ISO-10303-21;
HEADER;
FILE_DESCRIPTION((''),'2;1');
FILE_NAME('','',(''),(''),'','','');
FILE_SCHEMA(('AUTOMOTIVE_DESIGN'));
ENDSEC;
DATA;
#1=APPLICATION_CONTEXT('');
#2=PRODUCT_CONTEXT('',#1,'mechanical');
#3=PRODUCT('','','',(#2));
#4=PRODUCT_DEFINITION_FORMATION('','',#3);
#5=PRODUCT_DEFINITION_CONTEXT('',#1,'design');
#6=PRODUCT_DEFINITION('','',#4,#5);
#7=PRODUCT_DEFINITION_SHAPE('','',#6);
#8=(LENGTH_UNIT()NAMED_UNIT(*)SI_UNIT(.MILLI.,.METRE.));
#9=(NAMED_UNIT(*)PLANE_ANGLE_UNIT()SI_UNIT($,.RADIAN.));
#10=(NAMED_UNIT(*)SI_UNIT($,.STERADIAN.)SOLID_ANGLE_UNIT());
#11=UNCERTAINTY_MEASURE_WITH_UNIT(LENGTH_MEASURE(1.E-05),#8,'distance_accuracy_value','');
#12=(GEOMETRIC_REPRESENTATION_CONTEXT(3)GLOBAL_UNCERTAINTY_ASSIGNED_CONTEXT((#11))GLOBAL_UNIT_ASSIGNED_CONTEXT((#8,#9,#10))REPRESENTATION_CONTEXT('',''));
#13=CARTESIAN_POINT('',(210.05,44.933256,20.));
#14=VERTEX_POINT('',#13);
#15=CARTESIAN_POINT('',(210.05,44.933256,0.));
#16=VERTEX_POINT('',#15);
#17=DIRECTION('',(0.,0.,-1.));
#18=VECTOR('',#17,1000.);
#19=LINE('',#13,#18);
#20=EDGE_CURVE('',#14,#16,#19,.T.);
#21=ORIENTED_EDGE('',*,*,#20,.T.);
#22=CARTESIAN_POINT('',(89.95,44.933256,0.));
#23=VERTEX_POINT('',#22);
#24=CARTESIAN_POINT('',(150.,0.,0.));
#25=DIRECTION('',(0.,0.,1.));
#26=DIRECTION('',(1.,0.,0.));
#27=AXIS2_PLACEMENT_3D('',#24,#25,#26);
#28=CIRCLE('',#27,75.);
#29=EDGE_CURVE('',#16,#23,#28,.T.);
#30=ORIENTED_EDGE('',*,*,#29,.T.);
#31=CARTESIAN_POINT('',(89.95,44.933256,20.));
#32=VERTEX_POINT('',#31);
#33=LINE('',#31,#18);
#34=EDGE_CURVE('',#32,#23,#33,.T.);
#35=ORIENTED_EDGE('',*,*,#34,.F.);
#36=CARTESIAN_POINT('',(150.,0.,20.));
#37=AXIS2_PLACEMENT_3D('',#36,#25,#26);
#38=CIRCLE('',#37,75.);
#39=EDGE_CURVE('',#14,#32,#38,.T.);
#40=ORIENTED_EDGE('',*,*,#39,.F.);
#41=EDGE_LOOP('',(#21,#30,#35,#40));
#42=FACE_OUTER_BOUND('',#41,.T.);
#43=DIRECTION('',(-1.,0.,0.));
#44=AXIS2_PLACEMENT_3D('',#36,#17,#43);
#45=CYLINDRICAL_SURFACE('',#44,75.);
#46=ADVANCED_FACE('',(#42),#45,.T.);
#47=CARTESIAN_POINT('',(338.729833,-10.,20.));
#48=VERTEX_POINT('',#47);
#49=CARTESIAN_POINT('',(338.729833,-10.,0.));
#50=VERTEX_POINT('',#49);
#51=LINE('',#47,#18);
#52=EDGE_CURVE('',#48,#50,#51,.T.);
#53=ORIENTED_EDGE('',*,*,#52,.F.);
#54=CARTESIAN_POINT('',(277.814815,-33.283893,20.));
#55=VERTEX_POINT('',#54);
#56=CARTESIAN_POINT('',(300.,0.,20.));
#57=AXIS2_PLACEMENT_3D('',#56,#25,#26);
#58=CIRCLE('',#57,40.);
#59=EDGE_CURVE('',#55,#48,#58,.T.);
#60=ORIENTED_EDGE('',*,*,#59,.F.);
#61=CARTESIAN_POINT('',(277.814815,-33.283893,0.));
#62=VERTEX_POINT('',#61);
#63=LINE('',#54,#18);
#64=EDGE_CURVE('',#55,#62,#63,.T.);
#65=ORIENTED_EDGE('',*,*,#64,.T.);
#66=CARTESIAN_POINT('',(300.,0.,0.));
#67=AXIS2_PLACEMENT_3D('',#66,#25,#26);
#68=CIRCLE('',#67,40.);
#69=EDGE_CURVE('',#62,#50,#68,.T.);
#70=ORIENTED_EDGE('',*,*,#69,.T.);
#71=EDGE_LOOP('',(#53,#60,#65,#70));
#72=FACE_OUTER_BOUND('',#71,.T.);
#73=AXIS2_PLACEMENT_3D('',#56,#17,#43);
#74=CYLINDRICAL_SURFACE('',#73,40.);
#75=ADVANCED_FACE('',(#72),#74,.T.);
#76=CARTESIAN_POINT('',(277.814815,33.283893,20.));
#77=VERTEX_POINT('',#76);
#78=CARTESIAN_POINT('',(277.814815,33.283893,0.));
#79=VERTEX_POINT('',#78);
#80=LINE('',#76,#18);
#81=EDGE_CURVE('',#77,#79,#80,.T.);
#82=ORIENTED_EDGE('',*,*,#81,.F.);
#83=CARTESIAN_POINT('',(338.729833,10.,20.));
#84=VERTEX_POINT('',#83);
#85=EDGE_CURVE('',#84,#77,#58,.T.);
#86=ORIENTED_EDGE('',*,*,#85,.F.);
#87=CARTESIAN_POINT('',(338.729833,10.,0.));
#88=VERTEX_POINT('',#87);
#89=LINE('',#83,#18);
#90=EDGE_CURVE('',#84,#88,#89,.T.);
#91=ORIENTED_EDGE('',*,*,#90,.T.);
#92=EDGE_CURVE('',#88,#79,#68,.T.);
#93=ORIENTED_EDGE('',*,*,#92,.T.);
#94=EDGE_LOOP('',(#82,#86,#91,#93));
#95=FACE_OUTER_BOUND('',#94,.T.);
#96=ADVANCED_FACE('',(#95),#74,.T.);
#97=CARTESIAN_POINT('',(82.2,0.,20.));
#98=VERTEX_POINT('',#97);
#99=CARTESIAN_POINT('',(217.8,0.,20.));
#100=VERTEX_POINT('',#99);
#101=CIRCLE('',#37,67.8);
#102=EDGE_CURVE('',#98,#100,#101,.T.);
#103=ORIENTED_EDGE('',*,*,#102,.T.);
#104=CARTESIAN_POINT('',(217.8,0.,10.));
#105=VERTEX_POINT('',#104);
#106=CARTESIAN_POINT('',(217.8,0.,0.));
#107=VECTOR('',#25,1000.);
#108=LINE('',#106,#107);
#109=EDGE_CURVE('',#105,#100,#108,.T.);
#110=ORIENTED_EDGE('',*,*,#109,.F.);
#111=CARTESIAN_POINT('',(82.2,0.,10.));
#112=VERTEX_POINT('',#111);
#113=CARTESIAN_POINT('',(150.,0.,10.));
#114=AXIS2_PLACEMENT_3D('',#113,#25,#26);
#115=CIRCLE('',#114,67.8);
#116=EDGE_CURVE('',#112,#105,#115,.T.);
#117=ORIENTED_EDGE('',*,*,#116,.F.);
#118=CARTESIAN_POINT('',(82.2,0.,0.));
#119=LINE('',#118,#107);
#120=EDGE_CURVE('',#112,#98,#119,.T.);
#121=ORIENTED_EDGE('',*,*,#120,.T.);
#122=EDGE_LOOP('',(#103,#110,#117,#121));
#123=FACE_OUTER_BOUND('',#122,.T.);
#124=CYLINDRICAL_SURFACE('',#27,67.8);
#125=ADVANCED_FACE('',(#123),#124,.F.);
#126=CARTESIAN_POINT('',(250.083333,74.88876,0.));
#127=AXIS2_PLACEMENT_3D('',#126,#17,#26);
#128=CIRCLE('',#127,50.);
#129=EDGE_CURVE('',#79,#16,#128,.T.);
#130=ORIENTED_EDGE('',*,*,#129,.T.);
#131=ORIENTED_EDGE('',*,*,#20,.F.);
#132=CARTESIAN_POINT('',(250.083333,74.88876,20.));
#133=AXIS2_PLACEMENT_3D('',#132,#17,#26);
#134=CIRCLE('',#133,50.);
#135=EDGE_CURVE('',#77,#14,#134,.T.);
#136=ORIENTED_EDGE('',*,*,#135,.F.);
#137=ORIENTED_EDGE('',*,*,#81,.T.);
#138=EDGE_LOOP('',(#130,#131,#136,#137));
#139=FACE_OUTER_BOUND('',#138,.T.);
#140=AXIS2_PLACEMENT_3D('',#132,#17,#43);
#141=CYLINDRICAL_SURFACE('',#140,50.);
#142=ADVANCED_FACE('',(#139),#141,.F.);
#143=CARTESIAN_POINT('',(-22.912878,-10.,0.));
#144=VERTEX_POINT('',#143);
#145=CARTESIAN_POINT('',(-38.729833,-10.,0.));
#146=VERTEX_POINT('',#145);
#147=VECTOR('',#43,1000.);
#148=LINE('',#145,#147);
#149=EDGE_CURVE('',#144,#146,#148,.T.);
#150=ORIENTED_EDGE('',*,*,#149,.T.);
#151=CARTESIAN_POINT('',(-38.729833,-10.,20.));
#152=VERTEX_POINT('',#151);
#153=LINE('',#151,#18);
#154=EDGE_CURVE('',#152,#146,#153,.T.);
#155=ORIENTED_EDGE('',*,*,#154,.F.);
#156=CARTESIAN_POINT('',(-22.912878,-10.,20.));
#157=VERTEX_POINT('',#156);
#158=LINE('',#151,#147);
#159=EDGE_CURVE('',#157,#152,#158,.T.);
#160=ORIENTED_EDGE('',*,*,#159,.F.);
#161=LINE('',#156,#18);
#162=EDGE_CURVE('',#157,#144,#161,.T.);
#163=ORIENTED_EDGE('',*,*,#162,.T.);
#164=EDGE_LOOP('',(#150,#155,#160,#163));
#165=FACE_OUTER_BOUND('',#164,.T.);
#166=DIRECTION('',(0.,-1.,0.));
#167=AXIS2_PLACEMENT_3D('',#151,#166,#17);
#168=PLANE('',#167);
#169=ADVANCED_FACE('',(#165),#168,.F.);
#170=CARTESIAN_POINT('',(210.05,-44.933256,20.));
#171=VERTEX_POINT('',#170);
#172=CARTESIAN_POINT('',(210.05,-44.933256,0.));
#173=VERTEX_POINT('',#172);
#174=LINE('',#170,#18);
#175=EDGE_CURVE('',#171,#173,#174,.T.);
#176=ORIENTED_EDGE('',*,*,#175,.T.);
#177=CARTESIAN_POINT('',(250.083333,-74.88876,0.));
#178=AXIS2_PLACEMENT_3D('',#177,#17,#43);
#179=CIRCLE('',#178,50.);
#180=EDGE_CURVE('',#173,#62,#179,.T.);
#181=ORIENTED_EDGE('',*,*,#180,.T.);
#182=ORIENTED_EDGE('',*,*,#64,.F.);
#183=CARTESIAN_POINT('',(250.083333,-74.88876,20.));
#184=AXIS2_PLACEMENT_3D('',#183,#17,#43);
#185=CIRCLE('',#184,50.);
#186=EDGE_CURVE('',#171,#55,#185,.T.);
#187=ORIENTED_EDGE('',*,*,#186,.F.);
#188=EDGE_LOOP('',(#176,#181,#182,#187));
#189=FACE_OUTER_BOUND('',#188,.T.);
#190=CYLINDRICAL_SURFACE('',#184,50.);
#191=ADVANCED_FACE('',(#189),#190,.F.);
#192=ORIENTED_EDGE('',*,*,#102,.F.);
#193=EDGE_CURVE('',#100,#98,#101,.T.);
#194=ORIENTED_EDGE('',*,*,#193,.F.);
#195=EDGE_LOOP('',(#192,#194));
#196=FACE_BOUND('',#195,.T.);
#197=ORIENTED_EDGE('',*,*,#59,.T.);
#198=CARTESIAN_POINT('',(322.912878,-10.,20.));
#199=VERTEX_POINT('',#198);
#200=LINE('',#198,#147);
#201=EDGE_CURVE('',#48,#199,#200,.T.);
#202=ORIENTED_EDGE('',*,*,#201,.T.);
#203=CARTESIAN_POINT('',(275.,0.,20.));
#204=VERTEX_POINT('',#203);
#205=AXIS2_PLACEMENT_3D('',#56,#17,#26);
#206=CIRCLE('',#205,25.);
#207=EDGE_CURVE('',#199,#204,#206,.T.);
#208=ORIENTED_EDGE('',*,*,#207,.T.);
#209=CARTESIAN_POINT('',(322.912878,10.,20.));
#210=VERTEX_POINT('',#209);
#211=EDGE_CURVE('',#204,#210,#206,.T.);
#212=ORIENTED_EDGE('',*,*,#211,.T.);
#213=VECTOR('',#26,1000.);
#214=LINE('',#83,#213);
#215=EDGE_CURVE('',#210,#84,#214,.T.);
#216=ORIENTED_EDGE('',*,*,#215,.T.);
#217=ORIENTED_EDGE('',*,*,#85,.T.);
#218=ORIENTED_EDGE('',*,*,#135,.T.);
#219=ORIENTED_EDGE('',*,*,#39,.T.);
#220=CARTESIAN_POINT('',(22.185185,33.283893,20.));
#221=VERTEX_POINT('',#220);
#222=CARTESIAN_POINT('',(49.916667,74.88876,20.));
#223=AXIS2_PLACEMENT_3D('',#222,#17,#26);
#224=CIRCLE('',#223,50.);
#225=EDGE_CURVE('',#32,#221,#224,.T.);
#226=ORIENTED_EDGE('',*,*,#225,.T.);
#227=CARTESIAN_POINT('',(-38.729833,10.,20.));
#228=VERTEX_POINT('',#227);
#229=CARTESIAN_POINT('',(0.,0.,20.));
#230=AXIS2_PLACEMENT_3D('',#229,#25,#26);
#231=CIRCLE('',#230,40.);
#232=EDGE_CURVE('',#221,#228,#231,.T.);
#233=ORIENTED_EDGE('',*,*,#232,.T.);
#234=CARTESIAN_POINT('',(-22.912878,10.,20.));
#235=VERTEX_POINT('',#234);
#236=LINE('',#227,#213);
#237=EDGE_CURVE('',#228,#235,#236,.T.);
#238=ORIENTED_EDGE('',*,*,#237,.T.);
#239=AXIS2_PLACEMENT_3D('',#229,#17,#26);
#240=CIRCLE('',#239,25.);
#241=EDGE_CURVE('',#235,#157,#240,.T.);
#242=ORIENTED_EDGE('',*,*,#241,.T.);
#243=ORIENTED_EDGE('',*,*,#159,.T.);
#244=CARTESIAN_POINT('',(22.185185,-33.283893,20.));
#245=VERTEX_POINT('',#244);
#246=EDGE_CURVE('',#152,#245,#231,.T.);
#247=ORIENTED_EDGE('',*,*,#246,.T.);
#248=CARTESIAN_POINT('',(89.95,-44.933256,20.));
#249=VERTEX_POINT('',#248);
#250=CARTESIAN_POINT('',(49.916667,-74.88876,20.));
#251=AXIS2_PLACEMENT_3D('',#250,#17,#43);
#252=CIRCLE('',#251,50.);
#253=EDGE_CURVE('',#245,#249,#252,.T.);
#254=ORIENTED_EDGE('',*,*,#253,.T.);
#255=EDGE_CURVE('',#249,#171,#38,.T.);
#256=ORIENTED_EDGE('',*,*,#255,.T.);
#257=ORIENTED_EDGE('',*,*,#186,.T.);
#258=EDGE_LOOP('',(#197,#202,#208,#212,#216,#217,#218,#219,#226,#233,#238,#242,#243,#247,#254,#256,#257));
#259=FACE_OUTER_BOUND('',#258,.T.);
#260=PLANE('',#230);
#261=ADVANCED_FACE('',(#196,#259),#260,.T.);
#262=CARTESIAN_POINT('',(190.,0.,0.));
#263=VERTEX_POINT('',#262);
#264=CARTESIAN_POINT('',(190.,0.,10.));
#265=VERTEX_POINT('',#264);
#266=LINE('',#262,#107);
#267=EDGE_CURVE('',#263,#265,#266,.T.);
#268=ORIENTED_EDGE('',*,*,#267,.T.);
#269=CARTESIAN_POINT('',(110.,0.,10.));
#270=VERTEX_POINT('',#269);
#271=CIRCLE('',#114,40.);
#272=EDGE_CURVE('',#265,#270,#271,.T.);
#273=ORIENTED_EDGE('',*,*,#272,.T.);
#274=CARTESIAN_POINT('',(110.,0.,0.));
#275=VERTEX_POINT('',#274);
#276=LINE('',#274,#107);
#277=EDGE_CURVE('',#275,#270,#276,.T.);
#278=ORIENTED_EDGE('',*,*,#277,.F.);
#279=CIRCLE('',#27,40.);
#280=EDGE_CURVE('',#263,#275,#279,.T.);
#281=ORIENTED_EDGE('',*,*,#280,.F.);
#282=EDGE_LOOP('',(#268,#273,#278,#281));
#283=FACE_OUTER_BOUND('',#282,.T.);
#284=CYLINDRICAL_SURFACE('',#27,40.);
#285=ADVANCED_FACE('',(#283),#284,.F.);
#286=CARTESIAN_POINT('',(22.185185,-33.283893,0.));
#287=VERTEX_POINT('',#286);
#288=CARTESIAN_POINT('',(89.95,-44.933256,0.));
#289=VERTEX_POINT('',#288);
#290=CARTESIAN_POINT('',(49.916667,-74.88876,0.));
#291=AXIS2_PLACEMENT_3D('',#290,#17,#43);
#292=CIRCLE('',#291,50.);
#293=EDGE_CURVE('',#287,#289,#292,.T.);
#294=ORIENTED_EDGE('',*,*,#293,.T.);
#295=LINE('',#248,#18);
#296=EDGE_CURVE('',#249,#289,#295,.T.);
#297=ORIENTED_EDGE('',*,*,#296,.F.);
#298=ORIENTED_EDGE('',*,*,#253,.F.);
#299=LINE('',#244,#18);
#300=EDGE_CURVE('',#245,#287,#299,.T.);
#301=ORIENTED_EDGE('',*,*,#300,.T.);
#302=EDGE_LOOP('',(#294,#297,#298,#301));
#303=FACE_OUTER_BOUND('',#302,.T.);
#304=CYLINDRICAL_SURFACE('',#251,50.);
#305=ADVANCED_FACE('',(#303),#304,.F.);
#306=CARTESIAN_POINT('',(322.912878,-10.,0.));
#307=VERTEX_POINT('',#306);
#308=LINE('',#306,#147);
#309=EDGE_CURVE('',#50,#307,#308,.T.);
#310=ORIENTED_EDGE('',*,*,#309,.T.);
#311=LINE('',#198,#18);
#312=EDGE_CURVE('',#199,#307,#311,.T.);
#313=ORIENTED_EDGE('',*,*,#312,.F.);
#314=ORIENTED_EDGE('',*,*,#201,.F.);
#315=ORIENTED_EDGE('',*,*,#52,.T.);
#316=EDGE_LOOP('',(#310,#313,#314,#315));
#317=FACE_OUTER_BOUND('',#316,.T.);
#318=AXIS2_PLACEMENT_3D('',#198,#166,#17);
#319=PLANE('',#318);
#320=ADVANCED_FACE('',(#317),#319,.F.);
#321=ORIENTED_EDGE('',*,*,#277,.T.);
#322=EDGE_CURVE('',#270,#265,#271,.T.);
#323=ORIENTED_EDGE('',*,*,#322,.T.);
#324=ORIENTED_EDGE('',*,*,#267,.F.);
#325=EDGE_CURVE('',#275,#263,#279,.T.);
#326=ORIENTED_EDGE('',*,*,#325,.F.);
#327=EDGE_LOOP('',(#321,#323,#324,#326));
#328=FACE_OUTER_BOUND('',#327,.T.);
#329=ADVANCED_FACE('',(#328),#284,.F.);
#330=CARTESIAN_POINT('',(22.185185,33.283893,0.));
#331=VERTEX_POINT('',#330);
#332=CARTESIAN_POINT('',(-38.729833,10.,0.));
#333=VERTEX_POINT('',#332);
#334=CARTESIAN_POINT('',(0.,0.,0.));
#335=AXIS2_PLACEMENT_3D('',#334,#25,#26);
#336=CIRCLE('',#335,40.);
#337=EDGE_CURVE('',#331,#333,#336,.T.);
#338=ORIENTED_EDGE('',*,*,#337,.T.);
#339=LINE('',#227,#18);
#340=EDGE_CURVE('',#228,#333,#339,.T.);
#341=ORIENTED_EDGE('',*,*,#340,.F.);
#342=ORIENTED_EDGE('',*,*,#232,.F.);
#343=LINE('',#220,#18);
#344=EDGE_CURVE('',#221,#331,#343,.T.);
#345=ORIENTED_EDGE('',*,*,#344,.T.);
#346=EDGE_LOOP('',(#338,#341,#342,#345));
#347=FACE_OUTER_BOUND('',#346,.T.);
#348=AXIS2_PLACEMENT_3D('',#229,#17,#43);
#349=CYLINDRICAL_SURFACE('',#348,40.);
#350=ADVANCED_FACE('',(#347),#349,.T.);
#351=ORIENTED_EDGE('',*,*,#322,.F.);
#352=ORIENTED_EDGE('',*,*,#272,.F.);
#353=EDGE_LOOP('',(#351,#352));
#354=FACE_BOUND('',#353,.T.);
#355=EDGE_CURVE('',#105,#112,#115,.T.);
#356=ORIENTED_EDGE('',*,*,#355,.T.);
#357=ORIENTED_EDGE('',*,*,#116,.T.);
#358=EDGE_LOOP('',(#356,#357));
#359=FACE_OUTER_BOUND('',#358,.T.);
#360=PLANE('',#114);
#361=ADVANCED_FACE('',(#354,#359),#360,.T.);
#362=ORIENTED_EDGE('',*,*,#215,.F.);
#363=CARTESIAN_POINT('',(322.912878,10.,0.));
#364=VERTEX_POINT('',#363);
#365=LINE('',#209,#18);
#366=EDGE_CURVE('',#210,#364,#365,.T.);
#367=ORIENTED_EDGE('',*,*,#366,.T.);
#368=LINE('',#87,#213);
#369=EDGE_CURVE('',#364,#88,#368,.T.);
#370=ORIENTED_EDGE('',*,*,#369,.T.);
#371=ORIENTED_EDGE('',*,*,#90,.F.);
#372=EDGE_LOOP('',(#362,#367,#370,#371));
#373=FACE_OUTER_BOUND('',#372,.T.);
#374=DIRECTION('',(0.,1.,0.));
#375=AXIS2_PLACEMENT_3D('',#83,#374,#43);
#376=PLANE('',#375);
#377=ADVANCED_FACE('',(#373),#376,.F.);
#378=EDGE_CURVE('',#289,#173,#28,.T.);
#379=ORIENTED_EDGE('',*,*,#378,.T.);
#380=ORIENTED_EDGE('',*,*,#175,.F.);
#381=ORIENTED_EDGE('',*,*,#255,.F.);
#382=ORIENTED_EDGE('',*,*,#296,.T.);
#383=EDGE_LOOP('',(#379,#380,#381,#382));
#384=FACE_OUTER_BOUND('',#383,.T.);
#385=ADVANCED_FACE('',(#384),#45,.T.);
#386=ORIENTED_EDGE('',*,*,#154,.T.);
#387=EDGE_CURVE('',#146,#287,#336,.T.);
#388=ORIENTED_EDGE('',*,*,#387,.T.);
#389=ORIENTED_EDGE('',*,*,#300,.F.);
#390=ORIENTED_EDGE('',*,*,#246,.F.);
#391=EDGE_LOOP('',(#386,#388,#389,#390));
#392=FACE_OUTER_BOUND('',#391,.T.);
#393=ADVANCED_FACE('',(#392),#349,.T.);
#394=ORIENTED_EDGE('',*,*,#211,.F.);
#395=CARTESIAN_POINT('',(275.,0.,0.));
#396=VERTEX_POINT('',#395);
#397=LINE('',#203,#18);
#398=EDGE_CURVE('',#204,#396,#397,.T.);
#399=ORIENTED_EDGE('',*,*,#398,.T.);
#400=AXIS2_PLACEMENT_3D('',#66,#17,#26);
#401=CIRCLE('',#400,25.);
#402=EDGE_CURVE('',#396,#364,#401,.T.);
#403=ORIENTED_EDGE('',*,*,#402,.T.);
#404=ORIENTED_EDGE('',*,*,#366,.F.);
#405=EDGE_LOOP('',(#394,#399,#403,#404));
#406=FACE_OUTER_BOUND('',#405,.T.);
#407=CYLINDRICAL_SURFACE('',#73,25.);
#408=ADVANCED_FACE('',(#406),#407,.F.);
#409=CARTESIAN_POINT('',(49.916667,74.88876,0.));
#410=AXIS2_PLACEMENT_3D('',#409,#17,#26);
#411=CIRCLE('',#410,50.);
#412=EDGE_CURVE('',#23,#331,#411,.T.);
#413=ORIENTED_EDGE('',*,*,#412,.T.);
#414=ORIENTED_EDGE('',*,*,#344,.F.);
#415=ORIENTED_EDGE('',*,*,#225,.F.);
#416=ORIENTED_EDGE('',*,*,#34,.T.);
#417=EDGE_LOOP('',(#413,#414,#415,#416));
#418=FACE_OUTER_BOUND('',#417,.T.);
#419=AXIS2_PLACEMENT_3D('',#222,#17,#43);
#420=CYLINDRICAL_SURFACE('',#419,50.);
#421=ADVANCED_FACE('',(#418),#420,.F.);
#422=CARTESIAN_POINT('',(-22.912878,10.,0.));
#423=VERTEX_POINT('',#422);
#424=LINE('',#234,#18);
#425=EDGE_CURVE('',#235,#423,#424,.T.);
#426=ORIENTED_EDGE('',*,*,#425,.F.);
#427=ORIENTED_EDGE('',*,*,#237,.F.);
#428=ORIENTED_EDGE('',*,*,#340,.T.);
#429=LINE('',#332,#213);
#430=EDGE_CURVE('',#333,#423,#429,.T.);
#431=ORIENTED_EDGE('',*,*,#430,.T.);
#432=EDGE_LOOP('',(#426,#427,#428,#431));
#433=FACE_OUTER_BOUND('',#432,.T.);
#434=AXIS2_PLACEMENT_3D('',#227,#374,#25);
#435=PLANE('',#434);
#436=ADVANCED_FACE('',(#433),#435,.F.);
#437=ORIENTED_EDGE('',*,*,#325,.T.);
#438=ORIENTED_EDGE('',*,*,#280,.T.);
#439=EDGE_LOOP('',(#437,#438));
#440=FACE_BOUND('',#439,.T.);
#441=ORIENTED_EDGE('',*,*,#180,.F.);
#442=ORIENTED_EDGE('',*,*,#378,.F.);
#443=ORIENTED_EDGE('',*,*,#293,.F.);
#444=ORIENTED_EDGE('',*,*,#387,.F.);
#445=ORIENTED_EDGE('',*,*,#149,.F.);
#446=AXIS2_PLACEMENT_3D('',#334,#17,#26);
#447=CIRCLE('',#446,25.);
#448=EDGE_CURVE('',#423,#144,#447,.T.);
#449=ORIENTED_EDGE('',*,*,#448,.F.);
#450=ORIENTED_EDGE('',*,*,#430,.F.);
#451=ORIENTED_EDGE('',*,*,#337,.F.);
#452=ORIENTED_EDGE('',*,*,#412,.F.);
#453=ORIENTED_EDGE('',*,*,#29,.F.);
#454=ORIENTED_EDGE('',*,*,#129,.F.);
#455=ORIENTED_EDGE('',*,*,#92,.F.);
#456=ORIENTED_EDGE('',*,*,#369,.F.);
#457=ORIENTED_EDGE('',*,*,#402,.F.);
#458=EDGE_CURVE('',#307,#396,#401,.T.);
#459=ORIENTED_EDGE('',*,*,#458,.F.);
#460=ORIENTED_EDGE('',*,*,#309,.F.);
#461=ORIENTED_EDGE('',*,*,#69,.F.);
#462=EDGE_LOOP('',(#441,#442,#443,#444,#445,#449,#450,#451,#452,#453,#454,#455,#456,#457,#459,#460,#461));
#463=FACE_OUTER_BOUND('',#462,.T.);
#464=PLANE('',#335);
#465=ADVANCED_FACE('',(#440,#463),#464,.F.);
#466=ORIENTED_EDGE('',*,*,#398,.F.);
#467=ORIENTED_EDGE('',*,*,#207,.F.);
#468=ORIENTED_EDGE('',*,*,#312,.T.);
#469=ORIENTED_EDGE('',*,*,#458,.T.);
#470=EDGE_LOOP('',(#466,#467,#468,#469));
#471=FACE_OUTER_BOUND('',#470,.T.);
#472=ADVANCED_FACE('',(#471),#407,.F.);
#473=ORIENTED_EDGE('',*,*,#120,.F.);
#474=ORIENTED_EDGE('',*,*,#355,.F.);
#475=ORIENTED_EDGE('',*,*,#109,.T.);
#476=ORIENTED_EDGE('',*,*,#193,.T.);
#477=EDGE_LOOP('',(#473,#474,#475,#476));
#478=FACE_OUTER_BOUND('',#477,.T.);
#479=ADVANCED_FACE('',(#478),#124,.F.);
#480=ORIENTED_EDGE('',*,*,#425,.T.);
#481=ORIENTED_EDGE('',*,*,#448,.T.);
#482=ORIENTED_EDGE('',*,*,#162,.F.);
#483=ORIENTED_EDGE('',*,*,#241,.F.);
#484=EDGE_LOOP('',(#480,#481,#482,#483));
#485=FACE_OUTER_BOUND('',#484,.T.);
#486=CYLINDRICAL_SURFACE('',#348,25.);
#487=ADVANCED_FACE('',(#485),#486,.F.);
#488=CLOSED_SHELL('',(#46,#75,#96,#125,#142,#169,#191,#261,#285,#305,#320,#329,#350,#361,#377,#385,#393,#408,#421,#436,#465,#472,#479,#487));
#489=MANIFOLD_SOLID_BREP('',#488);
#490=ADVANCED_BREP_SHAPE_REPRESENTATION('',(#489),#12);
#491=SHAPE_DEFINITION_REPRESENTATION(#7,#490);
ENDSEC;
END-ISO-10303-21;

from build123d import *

# Parameters (mm, degrees)
LINK_PLATE_20MM_DEPTH       = 20
CENTRE_OPENING_SKETCH_R     = 67.8
CENTRE_OPENING_135_6_DEPTH  = 20
ANNULAR_WEB_SKETCH_R        = 67.8
ANNULAR_WEB_SKETCH_R_2      = 40
ANNULAR_WEB_80X_135_6_DEPTH = 10


with BuildPart() as part:
    # Link Plate Outline Sketch → Link Plate 20mm (new body)
    with BuildSketch(Plane.XY):
        with BuildLine():
            Line((-38.729833462, 10), (-22.912878475, 10))
            ThreePointArc((-22.912878475, 10), (25, 0), (-22.912878475, -10))
            Line((-22.912878475, -10), (-38.729833462, -10))
            ThreePointArc((-38.729833462, -10), (-14.281675999, -37.363534772), (22.185185185, -33.283893377))
            ThreePointArc((22.185185185, -33.283893377), (58.387841465, -25.611592996), (89.95, -44.933256058))
            ThreePointArc((89.95, -44.933256058), (150, -75), (210.05, -44.933256058))
            ThreePointArc((210.05, -44.933256058), (241.612158535, -25.611592996), (277.814814815, -33.283893377))
            ThreePointArc((277.814814815, -33.283893377), (314.281675999, -37.363534772), (338.729833462, -10))
            Line((338.729833462, -10), (322.912878475, -10))
            ThreePointArc((322.912878475, -10), (275, 0), (322.912878475, 10))
            Line((322.912878475, 10), (338.729833462, 10))
            ThreePointArc((338.729833462, 10), (314.281675999, 37.363534772), (277.814814815, 33.283893377))
            ThreePointArc((277.814814815, 33.283893377), (241.612158535, 25.611592996), (210.05, 44.933256058))
            ThreePointArc((210.05, 44.933256058), (150, 75), (89.95, 44.933256058))
            ThreePointArc((89.95, 44.933256058), (58.387841465, 25.611592996), (22.185185185, 33.283893377))
            ThreePointArc((22.185185185, 33.283893377), (-14.281675999, 37.363534772), (-38.729833462, 10))
        make_face()
    extrude(amount=LINK_PLATE_20MM_DEPTH)

    # Centre Opening Sketch → Centre Opening Ø135.6 (cut)
    with BuildSketch(Plane.XY.offset(20)):
        with Locations((150, 0)):
            Circle(CENTRE_OPENING_SKETCH_R)
    extrude(amount=-CENTRE_OPENING_135_6_DEPTH, mode=Mode.SUBTRACT)

    # Annular Web Sketch → Annular Web Ø80xØ135.6 (add)
    with BuildSketch(Plane.XY.offset(10)):
        with Locations((150, 0)):
            Circle(ANNULAR_WEB_SKETCH_R)
        with Locations((150, 0)):
            Circle(ANNULAR_WEB_SKETCH_R_2, mode=Mode.SUBTRACT)
    extrude(amount=-ANNULAR_WEB_80X_135_6_DEPTH)


solid = part.part
